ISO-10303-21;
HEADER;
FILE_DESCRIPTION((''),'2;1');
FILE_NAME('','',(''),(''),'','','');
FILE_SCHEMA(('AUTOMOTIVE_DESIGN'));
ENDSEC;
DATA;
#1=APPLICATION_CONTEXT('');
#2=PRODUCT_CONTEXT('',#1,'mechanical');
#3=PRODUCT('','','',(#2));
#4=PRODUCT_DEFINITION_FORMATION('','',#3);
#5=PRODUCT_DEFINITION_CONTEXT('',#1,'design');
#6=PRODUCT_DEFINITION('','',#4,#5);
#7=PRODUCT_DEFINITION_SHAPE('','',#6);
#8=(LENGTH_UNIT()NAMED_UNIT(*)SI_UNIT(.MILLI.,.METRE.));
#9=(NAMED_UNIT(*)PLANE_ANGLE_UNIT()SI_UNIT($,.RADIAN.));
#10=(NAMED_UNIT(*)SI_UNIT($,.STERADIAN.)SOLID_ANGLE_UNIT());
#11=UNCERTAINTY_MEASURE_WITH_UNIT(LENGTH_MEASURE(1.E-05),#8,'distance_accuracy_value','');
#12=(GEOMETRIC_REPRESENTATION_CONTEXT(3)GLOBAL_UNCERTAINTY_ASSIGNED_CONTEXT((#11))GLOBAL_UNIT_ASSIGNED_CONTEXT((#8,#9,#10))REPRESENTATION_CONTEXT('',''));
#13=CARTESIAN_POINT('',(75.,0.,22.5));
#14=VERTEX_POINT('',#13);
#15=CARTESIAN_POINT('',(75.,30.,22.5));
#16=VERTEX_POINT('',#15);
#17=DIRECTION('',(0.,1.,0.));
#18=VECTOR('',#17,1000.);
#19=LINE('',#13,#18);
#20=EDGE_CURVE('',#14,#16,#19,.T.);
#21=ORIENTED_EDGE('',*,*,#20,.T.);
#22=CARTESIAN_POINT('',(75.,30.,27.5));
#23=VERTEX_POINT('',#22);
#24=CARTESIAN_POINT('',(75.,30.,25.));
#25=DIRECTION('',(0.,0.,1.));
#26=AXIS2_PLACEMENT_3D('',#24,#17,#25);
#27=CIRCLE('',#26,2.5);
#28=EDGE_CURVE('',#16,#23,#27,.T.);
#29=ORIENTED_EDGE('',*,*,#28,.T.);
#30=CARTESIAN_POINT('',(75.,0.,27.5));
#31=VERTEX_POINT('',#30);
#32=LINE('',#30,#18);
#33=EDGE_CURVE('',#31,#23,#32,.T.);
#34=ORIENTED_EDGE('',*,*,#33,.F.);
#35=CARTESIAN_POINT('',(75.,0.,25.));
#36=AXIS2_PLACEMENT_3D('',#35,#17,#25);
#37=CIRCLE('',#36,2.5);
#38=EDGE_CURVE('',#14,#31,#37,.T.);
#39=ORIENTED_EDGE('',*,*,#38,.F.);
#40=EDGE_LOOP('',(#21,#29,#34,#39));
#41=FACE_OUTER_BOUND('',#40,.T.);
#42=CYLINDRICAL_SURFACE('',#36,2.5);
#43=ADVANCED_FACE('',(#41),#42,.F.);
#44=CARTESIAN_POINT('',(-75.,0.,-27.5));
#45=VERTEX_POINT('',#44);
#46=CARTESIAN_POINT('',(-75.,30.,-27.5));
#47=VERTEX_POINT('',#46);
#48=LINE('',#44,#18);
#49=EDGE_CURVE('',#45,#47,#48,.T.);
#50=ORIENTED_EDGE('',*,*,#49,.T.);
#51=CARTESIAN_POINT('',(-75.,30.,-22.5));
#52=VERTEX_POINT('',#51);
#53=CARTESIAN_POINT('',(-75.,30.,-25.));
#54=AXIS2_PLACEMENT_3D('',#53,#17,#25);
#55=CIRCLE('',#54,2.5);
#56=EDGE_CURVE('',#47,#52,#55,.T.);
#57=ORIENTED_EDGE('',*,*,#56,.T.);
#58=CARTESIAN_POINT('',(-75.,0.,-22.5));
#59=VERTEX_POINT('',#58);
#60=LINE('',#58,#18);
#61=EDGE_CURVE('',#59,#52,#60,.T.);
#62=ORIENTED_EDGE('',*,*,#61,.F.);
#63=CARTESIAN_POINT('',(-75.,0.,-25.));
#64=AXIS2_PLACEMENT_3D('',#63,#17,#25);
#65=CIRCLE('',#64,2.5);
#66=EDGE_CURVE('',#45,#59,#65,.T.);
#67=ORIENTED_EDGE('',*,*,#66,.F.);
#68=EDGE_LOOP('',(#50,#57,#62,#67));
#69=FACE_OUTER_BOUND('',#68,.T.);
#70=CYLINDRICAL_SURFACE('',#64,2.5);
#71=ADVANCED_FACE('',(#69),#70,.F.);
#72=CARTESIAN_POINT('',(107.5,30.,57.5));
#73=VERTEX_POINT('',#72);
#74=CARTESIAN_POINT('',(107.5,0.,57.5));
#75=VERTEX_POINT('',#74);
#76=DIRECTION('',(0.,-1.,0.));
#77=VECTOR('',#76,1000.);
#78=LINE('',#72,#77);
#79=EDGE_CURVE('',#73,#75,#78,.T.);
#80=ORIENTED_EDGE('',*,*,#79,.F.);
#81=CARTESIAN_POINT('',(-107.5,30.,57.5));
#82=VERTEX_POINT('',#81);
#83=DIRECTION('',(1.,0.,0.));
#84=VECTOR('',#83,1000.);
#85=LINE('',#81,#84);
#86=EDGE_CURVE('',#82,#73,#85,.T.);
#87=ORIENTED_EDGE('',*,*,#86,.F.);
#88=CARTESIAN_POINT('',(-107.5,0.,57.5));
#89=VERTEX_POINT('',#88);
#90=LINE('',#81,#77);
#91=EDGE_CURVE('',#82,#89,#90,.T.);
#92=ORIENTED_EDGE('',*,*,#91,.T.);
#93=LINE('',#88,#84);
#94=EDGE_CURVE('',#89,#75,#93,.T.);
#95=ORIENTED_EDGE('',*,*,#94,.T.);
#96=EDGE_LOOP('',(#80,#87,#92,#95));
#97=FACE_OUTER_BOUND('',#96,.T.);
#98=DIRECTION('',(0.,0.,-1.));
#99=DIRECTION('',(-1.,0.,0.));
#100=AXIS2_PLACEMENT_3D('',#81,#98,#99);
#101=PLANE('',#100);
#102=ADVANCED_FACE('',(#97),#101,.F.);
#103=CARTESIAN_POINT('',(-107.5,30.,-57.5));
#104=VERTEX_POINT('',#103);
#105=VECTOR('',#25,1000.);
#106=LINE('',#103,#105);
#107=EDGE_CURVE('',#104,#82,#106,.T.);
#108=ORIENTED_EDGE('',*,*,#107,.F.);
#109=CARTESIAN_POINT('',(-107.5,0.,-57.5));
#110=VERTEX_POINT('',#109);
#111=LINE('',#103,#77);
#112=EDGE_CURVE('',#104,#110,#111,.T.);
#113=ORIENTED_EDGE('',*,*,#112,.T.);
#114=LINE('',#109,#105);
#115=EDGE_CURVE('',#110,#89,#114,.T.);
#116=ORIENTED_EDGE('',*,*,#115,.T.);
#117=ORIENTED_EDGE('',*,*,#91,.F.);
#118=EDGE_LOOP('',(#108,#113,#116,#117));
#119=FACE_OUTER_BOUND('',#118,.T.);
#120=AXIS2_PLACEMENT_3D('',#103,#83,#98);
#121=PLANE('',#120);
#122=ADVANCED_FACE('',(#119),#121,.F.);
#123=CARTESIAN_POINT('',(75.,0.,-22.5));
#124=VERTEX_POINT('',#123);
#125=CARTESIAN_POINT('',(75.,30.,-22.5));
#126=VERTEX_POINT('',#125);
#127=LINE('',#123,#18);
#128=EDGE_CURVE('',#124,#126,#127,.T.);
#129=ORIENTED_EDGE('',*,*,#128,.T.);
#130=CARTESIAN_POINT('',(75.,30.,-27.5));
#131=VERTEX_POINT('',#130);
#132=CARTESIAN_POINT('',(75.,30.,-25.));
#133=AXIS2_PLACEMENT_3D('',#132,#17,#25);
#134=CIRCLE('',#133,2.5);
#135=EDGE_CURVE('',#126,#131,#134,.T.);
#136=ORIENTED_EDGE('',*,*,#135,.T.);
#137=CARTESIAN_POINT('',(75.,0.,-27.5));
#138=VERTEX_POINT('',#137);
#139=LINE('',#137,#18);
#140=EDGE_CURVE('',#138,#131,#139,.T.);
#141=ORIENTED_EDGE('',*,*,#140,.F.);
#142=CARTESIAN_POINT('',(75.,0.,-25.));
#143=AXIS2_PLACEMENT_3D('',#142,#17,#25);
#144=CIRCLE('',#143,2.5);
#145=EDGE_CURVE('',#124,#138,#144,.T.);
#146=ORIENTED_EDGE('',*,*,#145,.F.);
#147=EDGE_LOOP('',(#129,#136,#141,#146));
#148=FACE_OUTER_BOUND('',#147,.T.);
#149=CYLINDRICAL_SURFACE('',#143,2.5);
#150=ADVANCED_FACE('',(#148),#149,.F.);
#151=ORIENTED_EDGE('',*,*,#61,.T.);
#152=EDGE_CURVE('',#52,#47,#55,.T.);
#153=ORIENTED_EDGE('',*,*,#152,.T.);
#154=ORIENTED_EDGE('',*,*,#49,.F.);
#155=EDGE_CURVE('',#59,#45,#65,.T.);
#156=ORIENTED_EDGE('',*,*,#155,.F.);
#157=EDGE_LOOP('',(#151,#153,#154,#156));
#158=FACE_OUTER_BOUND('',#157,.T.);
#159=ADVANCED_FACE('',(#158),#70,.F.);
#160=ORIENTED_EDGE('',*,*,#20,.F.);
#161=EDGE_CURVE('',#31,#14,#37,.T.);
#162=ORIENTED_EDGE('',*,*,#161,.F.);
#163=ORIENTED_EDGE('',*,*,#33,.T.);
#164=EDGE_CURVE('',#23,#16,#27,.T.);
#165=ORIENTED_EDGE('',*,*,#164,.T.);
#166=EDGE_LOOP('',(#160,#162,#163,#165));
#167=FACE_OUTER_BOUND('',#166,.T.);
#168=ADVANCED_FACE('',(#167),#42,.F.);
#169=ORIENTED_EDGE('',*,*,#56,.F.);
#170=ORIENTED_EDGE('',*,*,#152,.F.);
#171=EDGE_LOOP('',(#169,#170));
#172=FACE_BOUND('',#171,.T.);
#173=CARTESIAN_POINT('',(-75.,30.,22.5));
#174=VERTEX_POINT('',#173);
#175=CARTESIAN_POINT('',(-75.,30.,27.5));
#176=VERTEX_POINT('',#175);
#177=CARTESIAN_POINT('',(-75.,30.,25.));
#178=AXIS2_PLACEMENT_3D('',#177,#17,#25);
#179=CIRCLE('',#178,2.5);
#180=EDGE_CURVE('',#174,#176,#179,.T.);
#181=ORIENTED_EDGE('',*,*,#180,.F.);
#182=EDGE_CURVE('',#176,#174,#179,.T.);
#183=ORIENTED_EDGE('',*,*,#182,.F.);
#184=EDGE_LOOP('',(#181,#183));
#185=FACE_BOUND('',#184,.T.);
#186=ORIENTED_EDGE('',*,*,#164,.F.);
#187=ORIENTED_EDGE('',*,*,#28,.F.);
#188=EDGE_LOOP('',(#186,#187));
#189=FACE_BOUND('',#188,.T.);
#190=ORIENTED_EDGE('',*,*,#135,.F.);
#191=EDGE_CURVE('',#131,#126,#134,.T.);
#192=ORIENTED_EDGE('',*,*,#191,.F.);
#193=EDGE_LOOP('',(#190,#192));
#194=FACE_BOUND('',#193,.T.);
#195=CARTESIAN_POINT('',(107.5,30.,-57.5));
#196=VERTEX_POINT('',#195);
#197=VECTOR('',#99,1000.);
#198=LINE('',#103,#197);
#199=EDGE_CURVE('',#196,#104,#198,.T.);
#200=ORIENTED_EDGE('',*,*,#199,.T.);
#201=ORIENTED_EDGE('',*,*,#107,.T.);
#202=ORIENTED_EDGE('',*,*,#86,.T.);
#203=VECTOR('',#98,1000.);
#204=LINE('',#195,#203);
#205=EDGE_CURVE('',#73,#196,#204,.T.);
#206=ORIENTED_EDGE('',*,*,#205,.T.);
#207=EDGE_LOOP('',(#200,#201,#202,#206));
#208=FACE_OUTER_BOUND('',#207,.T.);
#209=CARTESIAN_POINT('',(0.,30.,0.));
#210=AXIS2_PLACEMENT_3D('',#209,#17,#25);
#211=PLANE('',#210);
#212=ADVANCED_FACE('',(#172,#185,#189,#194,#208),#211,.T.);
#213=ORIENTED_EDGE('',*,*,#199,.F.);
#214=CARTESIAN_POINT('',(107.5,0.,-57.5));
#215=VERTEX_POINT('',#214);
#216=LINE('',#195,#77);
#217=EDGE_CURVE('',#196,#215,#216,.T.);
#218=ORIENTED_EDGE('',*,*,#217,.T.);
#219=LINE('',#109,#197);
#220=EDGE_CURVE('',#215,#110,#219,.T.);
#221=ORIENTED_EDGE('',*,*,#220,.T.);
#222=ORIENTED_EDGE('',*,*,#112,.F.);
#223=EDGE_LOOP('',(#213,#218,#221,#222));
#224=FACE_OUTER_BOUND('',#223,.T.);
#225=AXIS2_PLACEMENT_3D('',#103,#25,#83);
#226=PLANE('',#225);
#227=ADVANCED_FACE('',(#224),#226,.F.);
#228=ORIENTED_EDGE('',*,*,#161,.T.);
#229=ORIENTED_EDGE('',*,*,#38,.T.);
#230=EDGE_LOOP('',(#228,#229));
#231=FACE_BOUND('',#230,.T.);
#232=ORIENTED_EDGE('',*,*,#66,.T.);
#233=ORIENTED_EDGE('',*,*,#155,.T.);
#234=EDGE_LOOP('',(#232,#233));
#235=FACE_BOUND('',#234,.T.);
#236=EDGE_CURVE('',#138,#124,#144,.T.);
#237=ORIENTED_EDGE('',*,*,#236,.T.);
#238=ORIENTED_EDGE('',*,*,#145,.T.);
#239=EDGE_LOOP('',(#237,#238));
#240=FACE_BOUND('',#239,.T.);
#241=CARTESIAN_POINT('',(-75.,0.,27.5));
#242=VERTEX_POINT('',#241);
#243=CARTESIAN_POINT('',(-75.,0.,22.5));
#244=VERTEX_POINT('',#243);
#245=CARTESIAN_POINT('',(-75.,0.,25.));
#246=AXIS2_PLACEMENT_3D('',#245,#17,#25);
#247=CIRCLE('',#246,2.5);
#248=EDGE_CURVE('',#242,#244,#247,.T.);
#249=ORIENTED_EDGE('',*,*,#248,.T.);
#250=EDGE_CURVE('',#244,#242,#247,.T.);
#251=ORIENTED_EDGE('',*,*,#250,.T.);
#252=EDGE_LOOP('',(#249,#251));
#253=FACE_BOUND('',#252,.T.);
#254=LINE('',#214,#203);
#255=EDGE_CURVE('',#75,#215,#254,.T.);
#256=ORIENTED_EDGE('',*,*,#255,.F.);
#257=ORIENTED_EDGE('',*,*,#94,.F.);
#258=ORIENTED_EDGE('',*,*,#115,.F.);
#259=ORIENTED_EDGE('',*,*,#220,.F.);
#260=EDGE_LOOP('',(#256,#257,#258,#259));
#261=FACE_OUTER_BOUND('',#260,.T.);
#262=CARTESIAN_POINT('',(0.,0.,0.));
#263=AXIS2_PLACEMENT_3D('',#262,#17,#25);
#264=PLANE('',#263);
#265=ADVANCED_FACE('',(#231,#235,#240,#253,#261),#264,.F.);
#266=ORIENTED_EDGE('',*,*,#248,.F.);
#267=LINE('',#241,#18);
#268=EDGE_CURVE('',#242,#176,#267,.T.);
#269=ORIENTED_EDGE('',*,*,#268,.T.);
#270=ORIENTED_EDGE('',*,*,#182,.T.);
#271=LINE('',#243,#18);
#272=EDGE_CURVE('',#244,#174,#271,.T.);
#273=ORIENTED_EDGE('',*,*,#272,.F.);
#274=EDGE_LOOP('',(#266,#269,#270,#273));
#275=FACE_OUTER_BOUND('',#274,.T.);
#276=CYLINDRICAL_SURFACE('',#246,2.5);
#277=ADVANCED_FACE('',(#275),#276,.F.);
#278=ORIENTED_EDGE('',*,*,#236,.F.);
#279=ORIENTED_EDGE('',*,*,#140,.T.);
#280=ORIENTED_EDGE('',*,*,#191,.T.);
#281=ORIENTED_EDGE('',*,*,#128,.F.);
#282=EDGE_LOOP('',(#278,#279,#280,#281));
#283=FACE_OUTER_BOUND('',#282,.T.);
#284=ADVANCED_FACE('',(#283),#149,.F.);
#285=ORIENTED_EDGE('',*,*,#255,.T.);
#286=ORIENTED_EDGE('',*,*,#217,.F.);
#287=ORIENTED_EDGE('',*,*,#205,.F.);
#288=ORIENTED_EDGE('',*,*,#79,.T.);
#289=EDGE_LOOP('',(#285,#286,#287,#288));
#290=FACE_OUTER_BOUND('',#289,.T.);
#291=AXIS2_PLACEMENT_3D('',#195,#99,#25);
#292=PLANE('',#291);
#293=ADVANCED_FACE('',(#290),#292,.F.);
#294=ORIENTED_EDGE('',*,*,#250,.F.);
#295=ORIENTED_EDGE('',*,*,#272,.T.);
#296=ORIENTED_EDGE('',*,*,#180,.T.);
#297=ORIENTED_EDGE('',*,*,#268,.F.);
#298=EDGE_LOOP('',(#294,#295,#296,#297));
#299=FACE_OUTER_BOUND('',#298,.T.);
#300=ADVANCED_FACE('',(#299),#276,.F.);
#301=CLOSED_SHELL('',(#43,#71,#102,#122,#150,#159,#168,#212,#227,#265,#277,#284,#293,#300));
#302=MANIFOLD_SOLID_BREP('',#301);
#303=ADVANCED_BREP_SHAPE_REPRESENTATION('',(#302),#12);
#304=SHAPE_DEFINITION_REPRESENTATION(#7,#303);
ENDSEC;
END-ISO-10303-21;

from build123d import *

# Parameters (mm, degrees)
SKETCH_1_W          = 215
SKETCH_1_H          = 115
EXTRUDE_1_DEPTH     = 30
SKETCH_2_R          = 2.5
CUT_EXTRUDE_1_DEPTH = 30


with BuildPart() as part:
    # 草图1 → 凸台-拉伸1 (new body)
    with BuildSketch(Plane(origin=(0, 0, 0), x_dir=(1, 0, 0), z_dir=(0, 1, 0))):
        Rectangle(SKETCH_1_W, SKETCH_1_H)
    extrude(amount=EXTRUDE_1_DEPTH)

    # 草图2 → 切除-拉伸1 (cut)
    with BuildSketch(Plane(origin=(0, 30, 0), x_dir=(1, 0, 0), z_dir=(0, 1, 0))):
        with Locations(Location((-75, 25, 0), (0, 0, 270))):
            Circle(SKETCH_2_R)
        with Locations(Location((75, 25, 0), (0, 0, 270))):
            Circle(SKETCH_2_R)
        with Locations(Location((75, -25, 0), (0, 0, 270))):
            Circle(SKETCH_2_R)
        with Locations(Location((-75, -25, 0), (0, 0, 270))):
            Circle(SKETCH_2_R)
    extrude(amount=-CUT_EXTRUDE_1_DEPTH, mode=Mode.SUBTRACT)


solid = part.part
